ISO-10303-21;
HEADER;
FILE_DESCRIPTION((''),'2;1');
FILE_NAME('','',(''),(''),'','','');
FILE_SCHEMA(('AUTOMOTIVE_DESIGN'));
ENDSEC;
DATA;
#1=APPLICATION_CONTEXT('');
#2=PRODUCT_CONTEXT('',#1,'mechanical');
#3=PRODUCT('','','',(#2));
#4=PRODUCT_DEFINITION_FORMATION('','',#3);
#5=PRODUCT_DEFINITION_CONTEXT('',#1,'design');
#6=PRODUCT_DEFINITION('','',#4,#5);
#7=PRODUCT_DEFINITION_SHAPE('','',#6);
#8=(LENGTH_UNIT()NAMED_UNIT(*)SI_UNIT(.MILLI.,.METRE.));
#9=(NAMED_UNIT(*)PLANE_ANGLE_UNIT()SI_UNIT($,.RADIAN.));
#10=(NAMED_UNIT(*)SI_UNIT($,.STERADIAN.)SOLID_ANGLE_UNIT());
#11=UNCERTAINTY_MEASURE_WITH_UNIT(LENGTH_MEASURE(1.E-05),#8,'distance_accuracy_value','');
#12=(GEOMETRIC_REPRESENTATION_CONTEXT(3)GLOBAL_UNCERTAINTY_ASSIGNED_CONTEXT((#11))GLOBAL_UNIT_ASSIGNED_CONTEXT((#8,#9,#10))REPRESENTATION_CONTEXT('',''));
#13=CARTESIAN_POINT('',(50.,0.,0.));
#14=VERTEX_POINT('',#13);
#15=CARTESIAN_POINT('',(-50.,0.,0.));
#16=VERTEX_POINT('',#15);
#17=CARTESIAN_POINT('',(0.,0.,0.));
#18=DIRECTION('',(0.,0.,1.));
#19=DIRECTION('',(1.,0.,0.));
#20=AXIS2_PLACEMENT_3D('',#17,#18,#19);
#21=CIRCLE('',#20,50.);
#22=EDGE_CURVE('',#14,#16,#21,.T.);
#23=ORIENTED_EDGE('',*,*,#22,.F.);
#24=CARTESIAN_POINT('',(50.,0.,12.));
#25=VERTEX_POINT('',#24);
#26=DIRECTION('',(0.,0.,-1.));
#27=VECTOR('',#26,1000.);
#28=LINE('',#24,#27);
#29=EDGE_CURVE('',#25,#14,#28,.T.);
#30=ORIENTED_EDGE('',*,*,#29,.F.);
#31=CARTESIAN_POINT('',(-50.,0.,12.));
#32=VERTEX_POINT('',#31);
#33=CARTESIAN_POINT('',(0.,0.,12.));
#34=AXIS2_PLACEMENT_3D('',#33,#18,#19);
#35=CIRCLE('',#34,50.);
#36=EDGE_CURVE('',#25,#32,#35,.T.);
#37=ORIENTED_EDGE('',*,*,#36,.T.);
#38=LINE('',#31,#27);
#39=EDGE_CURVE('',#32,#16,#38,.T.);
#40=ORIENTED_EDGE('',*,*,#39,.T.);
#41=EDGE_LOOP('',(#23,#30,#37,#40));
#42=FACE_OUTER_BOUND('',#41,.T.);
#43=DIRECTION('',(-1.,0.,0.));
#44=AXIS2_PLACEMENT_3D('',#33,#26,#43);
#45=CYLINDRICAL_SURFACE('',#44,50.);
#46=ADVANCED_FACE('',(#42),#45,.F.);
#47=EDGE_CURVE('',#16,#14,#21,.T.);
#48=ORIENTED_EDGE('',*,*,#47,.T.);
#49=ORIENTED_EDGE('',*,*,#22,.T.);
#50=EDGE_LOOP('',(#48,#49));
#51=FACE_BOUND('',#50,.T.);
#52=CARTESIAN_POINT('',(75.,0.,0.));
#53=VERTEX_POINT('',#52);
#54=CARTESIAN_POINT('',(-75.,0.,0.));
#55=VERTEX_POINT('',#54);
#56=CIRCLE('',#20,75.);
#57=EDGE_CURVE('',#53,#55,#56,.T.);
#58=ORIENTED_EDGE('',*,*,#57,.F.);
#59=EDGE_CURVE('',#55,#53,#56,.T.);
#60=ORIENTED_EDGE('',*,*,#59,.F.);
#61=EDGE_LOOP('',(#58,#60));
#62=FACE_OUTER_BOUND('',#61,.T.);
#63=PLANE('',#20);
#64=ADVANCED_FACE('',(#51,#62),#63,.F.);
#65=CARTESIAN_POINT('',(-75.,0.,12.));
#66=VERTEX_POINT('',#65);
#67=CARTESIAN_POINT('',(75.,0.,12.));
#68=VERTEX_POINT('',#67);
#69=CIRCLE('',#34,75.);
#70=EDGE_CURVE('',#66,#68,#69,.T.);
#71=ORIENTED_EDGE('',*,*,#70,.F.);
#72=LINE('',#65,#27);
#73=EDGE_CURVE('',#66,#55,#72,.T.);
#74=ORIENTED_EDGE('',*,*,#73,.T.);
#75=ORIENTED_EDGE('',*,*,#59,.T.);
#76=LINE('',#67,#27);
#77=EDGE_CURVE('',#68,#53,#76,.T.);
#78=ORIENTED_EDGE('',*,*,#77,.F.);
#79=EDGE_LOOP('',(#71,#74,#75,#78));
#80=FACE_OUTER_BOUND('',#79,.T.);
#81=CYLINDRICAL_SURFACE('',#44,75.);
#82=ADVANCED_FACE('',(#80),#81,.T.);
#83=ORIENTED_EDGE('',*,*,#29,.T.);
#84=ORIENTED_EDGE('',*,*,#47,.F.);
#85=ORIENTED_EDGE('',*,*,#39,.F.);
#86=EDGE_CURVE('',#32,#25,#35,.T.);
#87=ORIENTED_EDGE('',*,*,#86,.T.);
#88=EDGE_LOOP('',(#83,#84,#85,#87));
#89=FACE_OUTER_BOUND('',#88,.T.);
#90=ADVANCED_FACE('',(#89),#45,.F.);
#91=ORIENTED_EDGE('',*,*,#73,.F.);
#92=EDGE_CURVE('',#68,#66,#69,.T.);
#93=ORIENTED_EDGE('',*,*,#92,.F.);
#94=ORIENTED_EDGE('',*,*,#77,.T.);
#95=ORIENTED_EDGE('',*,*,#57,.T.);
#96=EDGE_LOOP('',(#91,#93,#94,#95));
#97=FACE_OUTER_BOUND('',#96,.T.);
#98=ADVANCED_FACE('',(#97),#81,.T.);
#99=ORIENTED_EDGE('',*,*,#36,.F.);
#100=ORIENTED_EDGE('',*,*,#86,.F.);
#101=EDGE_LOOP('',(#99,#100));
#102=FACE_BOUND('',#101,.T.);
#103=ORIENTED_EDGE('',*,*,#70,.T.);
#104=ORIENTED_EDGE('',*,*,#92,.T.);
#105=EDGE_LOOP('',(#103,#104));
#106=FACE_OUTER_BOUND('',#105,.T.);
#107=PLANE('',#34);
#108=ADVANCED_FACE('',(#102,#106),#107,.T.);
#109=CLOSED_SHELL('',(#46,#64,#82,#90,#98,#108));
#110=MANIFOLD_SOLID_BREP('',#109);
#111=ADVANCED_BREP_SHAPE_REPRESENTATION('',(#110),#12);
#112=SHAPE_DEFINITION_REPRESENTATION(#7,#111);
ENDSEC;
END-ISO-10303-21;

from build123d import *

# Parameters (mm, degrees)
SKETCH1_R           = 75
SKETCH1_R_2         = 50
BOSS_EXTRUDE1_DEPTH = 12


with BuildPart() as part:
    # Sketch1 → Boss-Extrude1 (new body)
    with BuildSketch(Plane.XY):
        Circle(SKETCH1_R)
        Circle(SKETCH1_R_2, mode=Mode.SUBTRACT)
    extrude(amount=BOSS_EXTRUDE1_DEPTH)


solid = part.part
